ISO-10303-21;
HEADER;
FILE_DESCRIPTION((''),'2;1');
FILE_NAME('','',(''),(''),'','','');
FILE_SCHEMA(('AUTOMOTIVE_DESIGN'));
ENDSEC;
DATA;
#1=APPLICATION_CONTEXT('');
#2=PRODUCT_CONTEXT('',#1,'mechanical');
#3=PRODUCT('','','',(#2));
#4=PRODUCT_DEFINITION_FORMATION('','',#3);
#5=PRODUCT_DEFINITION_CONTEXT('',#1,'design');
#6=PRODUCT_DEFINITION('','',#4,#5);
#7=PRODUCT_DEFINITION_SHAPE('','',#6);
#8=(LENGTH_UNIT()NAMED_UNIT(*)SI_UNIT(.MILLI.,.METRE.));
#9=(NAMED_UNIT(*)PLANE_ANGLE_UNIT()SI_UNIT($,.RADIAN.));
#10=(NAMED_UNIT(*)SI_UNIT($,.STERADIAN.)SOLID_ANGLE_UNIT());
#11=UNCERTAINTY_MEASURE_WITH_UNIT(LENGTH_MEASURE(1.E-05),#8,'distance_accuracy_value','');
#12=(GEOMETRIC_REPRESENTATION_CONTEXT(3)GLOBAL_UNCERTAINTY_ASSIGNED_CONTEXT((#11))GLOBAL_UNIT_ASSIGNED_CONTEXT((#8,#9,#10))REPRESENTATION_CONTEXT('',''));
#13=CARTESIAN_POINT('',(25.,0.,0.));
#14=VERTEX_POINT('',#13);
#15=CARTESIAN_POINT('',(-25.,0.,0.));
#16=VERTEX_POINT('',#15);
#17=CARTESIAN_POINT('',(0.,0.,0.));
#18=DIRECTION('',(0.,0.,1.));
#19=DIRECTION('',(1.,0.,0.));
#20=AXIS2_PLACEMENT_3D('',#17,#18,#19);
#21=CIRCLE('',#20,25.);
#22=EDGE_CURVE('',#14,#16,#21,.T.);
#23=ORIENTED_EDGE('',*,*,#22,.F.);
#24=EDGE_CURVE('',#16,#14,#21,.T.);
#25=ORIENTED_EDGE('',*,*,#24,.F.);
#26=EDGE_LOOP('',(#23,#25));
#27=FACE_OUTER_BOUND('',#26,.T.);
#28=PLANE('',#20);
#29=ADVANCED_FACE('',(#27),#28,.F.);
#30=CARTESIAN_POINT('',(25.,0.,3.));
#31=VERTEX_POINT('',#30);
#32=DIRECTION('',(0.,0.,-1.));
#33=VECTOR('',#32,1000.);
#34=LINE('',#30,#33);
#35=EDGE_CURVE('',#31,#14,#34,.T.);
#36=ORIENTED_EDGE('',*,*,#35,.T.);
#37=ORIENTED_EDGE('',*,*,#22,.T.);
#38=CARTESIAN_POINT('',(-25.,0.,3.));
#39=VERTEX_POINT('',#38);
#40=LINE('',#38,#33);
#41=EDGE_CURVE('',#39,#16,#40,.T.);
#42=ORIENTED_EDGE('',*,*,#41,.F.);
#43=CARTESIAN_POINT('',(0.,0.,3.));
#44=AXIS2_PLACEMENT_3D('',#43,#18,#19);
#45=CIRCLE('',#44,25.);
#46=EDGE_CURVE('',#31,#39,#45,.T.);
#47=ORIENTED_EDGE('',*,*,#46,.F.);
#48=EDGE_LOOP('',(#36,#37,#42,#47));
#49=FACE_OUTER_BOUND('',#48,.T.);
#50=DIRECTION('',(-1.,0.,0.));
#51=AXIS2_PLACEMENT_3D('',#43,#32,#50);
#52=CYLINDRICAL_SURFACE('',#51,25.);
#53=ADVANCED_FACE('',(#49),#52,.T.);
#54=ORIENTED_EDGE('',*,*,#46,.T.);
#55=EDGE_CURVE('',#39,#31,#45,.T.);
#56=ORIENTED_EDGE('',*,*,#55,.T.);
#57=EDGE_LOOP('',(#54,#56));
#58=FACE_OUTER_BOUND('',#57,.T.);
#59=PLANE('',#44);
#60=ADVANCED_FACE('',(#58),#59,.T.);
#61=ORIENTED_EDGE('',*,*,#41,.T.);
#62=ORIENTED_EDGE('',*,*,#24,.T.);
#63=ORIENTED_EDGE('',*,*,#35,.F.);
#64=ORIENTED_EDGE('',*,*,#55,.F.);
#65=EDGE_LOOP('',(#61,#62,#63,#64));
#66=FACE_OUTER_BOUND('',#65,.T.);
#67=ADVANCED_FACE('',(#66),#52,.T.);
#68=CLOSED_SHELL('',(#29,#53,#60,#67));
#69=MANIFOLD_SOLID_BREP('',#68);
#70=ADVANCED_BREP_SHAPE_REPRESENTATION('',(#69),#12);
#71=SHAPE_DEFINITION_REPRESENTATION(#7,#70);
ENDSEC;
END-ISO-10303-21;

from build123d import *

# Parameters (mm, degrees)
SKETCH1_R           = 25
BOSS_EXTRUDE1_DEPTH = 3


with BuildPart() as part:
    # Sketch1 → Boss-Extrude1 (new body)
    with BuildSketch(Plane.XY):
        Circle(SKETCH1_R)
    extrude(amount=BOSS_EXTRUDE1_DEPTH)


solid = part.part
